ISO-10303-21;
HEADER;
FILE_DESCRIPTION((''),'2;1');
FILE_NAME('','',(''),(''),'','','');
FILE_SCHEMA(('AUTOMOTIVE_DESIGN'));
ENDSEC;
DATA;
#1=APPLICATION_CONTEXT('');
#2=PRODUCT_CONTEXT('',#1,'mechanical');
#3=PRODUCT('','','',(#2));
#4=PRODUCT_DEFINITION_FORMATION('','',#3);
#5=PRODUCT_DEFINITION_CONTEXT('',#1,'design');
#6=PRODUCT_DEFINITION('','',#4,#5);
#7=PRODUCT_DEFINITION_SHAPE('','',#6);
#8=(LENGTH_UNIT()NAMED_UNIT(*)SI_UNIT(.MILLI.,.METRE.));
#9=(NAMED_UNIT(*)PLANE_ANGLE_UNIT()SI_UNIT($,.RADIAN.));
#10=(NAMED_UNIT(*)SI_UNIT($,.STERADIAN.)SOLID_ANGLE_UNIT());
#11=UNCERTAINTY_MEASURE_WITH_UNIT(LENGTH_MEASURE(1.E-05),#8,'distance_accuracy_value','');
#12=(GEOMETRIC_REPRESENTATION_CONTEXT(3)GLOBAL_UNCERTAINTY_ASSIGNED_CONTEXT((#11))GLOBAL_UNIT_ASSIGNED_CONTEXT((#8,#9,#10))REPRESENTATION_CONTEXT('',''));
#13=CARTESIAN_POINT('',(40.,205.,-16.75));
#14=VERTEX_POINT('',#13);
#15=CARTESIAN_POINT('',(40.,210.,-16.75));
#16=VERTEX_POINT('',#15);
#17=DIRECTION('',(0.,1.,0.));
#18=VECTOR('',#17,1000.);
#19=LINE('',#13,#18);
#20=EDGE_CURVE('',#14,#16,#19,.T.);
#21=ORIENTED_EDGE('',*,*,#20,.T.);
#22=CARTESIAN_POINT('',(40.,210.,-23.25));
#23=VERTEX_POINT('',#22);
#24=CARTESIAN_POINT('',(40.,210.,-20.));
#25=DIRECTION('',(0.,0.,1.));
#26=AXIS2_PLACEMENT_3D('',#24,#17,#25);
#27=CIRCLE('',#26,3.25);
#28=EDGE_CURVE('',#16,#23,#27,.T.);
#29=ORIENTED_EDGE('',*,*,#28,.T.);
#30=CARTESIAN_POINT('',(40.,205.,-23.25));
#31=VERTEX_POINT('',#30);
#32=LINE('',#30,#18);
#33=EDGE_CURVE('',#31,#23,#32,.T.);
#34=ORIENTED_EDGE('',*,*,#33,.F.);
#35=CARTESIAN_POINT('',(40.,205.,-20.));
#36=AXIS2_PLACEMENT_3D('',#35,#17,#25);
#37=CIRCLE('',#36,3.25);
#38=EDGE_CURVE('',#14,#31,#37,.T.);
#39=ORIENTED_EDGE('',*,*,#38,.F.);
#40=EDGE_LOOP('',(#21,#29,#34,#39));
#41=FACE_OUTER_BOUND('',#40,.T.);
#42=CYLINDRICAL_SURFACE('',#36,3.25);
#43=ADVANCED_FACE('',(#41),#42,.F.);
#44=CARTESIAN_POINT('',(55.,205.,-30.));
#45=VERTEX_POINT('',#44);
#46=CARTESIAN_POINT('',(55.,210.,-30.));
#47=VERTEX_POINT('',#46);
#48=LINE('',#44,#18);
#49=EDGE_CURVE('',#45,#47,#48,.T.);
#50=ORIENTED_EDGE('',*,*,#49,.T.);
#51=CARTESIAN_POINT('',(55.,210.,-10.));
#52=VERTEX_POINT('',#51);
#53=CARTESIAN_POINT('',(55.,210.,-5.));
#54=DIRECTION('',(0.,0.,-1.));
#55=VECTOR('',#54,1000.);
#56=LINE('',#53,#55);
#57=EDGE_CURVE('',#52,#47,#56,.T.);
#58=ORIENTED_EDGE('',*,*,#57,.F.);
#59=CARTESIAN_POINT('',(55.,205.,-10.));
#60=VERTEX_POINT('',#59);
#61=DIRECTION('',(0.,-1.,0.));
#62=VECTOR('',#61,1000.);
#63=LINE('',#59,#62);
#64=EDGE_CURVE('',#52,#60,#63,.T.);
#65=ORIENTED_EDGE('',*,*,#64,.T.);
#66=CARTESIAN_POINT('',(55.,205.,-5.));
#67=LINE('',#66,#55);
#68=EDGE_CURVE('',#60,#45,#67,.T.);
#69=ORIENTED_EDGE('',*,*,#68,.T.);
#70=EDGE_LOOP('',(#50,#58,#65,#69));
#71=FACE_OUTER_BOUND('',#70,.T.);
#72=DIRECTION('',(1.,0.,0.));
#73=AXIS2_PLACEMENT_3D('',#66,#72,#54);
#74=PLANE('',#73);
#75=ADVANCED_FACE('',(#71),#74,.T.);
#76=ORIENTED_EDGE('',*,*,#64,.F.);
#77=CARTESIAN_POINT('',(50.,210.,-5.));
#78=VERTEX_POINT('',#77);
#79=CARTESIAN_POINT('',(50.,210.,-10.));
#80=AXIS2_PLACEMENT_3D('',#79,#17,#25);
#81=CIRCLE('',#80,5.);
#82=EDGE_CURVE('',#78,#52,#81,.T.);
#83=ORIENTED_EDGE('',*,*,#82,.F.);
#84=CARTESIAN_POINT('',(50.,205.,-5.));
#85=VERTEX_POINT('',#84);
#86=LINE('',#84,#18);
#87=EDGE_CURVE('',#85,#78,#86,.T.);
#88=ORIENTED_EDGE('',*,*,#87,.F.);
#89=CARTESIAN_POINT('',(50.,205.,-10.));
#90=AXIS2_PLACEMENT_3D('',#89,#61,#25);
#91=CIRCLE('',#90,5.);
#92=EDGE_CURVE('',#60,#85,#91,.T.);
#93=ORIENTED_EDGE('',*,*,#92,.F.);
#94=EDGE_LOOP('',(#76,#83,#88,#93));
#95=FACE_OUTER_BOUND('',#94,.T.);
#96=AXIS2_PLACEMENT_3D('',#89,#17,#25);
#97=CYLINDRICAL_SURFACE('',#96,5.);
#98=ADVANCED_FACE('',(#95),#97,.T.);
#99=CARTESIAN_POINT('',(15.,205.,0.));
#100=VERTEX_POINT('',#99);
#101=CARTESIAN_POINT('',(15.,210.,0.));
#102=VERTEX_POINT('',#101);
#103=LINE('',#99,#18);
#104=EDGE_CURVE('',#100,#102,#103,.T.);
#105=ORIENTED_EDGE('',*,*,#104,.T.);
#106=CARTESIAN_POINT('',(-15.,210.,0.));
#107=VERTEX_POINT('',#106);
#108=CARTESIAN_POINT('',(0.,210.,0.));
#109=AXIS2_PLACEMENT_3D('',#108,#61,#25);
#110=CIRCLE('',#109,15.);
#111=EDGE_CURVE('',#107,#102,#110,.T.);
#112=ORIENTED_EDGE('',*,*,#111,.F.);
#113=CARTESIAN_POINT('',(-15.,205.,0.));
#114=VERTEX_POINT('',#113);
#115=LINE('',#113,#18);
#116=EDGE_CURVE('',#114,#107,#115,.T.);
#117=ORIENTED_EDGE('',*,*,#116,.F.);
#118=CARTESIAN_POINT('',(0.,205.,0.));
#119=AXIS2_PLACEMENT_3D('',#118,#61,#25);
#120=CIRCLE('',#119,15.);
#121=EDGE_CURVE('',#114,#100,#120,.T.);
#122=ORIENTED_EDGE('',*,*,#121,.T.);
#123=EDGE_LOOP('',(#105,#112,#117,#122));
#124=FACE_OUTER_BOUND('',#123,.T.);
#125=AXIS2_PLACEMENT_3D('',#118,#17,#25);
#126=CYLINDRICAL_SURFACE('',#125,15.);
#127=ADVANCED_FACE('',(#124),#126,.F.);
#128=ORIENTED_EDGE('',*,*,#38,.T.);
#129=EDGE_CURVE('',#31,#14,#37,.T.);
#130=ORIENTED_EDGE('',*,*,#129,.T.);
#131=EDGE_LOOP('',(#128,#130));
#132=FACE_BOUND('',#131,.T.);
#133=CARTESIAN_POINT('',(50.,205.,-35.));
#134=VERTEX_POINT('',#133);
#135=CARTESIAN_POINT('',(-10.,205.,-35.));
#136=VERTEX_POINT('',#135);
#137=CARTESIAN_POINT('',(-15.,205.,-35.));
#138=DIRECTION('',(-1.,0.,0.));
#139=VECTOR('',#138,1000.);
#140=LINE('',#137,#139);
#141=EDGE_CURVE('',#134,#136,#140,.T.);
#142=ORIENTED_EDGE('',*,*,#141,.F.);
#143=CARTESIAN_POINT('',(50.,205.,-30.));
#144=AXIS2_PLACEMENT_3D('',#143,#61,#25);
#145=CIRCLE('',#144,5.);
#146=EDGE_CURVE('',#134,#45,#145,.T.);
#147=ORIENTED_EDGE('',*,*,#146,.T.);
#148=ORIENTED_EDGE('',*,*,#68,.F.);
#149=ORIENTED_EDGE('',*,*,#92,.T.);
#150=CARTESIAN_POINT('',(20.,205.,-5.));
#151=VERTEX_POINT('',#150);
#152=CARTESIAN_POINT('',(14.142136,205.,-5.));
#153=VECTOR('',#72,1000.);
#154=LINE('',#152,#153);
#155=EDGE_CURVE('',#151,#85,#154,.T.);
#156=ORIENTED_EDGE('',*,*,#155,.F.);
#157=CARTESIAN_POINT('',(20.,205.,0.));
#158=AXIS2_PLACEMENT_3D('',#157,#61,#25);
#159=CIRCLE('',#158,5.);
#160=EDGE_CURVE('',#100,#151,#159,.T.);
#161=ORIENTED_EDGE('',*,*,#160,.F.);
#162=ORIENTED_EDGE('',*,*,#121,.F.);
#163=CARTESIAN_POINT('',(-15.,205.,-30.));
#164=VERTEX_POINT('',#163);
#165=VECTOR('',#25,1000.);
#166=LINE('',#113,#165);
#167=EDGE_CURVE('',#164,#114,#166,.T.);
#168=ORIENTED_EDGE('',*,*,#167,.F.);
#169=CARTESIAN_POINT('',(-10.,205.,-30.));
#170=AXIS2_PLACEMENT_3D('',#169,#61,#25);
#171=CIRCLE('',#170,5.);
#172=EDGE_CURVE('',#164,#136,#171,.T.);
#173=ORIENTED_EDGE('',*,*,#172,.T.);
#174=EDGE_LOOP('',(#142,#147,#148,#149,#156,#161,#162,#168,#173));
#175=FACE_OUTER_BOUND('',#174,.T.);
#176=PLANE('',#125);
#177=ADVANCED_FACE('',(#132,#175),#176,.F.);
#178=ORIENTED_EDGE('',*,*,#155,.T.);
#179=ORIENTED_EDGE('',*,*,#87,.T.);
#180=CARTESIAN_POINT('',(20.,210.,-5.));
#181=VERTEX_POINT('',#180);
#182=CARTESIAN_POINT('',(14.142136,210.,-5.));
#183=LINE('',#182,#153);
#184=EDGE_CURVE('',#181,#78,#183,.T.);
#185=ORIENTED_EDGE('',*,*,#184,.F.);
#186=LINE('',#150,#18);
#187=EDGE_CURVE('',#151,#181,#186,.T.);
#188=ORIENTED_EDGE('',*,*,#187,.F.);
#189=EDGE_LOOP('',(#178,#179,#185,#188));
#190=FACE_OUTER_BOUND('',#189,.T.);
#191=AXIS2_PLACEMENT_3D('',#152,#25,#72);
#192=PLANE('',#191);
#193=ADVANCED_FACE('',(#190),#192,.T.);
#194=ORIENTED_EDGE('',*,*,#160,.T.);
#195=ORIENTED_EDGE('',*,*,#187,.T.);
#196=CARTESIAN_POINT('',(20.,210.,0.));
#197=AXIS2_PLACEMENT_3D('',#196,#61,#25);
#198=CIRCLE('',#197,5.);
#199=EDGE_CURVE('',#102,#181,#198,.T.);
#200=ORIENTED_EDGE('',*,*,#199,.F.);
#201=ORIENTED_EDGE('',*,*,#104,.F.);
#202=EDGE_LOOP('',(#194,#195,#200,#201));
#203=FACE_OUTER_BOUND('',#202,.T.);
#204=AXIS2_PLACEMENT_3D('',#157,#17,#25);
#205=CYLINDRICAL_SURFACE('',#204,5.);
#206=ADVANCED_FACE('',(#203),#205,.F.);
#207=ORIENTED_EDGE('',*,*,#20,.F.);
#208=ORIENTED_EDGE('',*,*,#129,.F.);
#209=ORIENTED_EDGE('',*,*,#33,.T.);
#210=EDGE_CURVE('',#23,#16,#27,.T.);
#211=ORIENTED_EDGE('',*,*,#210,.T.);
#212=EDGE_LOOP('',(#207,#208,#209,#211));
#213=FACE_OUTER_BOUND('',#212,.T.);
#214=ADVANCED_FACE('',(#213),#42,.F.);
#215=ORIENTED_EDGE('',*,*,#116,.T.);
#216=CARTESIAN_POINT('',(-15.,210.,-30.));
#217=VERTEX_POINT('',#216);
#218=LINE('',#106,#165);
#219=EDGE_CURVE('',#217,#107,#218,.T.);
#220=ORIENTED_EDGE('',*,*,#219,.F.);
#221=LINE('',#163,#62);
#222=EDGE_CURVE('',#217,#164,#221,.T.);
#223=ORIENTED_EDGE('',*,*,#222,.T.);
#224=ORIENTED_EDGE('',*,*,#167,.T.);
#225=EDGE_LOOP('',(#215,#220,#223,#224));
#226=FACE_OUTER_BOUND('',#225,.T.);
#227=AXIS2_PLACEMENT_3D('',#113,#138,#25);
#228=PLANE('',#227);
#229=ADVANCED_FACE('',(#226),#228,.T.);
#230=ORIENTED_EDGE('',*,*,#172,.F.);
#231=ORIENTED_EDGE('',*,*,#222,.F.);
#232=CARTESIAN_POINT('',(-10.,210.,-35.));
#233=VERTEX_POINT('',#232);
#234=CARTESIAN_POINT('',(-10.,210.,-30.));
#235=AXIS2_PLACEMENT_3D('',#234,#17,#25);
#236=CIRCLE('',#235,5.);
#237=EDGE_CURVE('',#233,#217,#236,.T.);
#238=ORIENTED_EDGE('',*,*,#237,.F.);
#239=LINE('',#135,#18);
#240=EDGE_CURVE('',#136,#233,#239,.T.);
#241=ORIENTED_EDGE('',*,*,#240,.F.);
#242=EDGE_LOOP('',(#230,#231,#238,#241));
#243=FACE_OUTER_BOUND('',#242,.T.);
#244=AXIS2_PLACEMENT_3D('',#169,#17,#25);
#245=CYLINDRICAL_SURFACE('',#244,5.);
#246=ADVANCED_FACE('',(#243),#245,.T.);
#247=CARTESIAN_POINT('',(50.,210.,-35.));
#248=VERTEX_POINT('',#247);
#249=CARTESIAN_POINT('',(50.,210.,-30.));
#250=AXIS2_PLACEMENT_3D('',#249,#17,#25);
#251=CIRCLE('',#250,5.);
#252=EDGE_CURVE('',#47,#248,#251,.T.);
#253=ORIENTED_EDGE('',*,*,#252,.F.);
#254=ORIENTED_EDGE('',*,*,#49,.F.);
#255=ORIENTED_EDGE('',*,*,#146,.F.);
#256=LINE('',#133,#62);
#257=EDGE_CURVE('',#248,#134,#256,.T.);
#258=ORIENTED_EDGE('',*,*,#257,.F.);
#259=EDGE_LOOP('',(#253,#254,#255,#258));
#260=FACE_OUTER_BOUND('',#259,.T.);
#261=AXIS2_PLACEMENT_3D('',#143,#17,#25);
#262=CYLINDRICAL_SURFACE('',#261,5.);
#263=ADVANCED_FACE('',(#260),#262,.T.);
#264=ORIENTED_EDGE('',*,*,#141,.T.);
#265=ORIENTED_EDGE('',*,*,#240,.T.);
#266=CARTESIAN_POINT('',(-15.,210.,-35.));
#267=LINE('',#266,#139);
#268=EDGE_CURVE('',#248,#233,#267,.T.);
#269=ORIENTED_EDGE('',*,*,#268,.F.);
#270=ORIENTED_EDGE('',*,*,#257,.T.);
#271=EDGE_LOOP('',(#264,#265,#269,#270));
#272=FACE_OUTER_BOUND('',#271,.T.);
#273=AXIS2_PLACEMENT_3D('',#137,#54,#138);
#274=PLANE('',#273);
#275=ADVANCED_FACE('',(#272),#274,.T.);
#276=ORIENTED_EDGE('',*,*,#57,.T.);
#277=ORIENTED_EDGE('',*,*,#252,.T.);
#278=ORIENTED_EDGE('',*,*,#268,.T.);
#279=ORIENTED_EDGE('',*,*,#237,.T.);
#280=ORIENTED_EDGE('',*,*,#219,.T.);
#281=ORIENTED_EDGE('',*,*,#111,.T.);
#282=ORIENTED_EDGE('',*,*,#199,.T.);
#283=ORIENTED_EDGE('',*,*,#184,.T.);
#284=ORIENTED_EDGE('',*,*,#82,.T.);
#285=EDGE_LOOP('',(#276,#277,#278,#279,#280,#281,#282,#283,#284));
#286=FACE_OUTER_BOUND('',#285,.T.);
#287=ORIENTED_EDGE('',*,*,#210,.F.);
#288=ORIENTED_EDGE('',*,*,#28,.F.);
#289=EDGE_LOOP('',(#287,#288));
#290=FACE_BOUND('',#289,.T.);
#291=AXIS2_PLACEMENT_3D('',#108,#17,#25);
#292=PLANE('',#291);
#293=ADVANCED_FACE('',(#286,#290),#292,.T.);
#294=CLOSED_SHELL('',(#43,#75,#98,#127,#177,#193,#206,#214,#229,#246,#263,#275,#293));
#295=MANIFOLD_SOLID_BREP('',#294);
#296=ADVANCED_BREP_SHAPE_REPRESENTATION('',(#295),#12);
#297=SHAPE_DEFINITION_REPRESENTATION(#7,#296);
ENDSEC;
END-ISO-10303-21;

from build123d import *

# Parameters (mm, degrees)
BOSS_EXTRUDE1_DEPTH = 5
FILLET1_R           = 5
SKETCH2_R           = 3.25
CUT_EXTRUDE1_DEPTH  = 5
BOSS_EXTRUDE2_DEPTH = 5


with BuildPart() as part:
    # Sketch1 → Boss-Extrude1 (new body)
    with BuildSketch(Plane(origin=(0, 210, 0), x_dir=(1, 0, 0), z_dir=(0, 1, 0))):
        with BuildLine():
            Line((-15, 0), (-15, 35))
            Line((-15, 35), (55, 35))
            Line((55, 35), (55, 5))
            Line((55, 5), (14.142135624, 5))
            ThreePointArc((14.142135624, 5), (-2.536529681, 14.783978395), (-15, 0))
        make_face()
    extrude(amount=-BOSS_EXTRUDE1_DEPTH)

    # Fillet1
    fillet1_edges = [part.edges().sort_by_distance(p)[0] for p in [
        (-15, 207.5, -35),
        (55, 207.5, -35),
        (55, 207.5, -5),
    ]]
    fillet(fillet1_edges, radius=FILLET1_R)

    # Sketch2 → Cut-Extrude1 (cut)
    with BuildSketch(Plane(origin=(0, 210, 0), x_dir=(1, 0, 0), z_dir=(0, 1, 0))):
        with Locations(Location((40, 20, 0), (0, 0, 270))):
            Circle(SKETCH2_R)
    extrude(amount=-CUT_EXTRUDE1_DEPTH, mode=Mode.SUBTRACT)

    # Sketch3 → Boss-Extrude2 (add)
    with BuildSketch(Plane(origin=(0, 210, 0), x_dir=(1, 0, 0), z_dir=(0, 1, 0))):
        with BuildLine():
            ThreePointArc((15, 0), (16.464466094, 3.535533906), (20, 5))
            Line((20, 5), (14.142135624, 5))
            ThreePointArc((14.142135624, 5), (14.783978395, 2.536529681), (15, 0))
        make_face()
    extrude(amount=-BOSS_EXTRUDE2_DEPTH)


solid = part.part
